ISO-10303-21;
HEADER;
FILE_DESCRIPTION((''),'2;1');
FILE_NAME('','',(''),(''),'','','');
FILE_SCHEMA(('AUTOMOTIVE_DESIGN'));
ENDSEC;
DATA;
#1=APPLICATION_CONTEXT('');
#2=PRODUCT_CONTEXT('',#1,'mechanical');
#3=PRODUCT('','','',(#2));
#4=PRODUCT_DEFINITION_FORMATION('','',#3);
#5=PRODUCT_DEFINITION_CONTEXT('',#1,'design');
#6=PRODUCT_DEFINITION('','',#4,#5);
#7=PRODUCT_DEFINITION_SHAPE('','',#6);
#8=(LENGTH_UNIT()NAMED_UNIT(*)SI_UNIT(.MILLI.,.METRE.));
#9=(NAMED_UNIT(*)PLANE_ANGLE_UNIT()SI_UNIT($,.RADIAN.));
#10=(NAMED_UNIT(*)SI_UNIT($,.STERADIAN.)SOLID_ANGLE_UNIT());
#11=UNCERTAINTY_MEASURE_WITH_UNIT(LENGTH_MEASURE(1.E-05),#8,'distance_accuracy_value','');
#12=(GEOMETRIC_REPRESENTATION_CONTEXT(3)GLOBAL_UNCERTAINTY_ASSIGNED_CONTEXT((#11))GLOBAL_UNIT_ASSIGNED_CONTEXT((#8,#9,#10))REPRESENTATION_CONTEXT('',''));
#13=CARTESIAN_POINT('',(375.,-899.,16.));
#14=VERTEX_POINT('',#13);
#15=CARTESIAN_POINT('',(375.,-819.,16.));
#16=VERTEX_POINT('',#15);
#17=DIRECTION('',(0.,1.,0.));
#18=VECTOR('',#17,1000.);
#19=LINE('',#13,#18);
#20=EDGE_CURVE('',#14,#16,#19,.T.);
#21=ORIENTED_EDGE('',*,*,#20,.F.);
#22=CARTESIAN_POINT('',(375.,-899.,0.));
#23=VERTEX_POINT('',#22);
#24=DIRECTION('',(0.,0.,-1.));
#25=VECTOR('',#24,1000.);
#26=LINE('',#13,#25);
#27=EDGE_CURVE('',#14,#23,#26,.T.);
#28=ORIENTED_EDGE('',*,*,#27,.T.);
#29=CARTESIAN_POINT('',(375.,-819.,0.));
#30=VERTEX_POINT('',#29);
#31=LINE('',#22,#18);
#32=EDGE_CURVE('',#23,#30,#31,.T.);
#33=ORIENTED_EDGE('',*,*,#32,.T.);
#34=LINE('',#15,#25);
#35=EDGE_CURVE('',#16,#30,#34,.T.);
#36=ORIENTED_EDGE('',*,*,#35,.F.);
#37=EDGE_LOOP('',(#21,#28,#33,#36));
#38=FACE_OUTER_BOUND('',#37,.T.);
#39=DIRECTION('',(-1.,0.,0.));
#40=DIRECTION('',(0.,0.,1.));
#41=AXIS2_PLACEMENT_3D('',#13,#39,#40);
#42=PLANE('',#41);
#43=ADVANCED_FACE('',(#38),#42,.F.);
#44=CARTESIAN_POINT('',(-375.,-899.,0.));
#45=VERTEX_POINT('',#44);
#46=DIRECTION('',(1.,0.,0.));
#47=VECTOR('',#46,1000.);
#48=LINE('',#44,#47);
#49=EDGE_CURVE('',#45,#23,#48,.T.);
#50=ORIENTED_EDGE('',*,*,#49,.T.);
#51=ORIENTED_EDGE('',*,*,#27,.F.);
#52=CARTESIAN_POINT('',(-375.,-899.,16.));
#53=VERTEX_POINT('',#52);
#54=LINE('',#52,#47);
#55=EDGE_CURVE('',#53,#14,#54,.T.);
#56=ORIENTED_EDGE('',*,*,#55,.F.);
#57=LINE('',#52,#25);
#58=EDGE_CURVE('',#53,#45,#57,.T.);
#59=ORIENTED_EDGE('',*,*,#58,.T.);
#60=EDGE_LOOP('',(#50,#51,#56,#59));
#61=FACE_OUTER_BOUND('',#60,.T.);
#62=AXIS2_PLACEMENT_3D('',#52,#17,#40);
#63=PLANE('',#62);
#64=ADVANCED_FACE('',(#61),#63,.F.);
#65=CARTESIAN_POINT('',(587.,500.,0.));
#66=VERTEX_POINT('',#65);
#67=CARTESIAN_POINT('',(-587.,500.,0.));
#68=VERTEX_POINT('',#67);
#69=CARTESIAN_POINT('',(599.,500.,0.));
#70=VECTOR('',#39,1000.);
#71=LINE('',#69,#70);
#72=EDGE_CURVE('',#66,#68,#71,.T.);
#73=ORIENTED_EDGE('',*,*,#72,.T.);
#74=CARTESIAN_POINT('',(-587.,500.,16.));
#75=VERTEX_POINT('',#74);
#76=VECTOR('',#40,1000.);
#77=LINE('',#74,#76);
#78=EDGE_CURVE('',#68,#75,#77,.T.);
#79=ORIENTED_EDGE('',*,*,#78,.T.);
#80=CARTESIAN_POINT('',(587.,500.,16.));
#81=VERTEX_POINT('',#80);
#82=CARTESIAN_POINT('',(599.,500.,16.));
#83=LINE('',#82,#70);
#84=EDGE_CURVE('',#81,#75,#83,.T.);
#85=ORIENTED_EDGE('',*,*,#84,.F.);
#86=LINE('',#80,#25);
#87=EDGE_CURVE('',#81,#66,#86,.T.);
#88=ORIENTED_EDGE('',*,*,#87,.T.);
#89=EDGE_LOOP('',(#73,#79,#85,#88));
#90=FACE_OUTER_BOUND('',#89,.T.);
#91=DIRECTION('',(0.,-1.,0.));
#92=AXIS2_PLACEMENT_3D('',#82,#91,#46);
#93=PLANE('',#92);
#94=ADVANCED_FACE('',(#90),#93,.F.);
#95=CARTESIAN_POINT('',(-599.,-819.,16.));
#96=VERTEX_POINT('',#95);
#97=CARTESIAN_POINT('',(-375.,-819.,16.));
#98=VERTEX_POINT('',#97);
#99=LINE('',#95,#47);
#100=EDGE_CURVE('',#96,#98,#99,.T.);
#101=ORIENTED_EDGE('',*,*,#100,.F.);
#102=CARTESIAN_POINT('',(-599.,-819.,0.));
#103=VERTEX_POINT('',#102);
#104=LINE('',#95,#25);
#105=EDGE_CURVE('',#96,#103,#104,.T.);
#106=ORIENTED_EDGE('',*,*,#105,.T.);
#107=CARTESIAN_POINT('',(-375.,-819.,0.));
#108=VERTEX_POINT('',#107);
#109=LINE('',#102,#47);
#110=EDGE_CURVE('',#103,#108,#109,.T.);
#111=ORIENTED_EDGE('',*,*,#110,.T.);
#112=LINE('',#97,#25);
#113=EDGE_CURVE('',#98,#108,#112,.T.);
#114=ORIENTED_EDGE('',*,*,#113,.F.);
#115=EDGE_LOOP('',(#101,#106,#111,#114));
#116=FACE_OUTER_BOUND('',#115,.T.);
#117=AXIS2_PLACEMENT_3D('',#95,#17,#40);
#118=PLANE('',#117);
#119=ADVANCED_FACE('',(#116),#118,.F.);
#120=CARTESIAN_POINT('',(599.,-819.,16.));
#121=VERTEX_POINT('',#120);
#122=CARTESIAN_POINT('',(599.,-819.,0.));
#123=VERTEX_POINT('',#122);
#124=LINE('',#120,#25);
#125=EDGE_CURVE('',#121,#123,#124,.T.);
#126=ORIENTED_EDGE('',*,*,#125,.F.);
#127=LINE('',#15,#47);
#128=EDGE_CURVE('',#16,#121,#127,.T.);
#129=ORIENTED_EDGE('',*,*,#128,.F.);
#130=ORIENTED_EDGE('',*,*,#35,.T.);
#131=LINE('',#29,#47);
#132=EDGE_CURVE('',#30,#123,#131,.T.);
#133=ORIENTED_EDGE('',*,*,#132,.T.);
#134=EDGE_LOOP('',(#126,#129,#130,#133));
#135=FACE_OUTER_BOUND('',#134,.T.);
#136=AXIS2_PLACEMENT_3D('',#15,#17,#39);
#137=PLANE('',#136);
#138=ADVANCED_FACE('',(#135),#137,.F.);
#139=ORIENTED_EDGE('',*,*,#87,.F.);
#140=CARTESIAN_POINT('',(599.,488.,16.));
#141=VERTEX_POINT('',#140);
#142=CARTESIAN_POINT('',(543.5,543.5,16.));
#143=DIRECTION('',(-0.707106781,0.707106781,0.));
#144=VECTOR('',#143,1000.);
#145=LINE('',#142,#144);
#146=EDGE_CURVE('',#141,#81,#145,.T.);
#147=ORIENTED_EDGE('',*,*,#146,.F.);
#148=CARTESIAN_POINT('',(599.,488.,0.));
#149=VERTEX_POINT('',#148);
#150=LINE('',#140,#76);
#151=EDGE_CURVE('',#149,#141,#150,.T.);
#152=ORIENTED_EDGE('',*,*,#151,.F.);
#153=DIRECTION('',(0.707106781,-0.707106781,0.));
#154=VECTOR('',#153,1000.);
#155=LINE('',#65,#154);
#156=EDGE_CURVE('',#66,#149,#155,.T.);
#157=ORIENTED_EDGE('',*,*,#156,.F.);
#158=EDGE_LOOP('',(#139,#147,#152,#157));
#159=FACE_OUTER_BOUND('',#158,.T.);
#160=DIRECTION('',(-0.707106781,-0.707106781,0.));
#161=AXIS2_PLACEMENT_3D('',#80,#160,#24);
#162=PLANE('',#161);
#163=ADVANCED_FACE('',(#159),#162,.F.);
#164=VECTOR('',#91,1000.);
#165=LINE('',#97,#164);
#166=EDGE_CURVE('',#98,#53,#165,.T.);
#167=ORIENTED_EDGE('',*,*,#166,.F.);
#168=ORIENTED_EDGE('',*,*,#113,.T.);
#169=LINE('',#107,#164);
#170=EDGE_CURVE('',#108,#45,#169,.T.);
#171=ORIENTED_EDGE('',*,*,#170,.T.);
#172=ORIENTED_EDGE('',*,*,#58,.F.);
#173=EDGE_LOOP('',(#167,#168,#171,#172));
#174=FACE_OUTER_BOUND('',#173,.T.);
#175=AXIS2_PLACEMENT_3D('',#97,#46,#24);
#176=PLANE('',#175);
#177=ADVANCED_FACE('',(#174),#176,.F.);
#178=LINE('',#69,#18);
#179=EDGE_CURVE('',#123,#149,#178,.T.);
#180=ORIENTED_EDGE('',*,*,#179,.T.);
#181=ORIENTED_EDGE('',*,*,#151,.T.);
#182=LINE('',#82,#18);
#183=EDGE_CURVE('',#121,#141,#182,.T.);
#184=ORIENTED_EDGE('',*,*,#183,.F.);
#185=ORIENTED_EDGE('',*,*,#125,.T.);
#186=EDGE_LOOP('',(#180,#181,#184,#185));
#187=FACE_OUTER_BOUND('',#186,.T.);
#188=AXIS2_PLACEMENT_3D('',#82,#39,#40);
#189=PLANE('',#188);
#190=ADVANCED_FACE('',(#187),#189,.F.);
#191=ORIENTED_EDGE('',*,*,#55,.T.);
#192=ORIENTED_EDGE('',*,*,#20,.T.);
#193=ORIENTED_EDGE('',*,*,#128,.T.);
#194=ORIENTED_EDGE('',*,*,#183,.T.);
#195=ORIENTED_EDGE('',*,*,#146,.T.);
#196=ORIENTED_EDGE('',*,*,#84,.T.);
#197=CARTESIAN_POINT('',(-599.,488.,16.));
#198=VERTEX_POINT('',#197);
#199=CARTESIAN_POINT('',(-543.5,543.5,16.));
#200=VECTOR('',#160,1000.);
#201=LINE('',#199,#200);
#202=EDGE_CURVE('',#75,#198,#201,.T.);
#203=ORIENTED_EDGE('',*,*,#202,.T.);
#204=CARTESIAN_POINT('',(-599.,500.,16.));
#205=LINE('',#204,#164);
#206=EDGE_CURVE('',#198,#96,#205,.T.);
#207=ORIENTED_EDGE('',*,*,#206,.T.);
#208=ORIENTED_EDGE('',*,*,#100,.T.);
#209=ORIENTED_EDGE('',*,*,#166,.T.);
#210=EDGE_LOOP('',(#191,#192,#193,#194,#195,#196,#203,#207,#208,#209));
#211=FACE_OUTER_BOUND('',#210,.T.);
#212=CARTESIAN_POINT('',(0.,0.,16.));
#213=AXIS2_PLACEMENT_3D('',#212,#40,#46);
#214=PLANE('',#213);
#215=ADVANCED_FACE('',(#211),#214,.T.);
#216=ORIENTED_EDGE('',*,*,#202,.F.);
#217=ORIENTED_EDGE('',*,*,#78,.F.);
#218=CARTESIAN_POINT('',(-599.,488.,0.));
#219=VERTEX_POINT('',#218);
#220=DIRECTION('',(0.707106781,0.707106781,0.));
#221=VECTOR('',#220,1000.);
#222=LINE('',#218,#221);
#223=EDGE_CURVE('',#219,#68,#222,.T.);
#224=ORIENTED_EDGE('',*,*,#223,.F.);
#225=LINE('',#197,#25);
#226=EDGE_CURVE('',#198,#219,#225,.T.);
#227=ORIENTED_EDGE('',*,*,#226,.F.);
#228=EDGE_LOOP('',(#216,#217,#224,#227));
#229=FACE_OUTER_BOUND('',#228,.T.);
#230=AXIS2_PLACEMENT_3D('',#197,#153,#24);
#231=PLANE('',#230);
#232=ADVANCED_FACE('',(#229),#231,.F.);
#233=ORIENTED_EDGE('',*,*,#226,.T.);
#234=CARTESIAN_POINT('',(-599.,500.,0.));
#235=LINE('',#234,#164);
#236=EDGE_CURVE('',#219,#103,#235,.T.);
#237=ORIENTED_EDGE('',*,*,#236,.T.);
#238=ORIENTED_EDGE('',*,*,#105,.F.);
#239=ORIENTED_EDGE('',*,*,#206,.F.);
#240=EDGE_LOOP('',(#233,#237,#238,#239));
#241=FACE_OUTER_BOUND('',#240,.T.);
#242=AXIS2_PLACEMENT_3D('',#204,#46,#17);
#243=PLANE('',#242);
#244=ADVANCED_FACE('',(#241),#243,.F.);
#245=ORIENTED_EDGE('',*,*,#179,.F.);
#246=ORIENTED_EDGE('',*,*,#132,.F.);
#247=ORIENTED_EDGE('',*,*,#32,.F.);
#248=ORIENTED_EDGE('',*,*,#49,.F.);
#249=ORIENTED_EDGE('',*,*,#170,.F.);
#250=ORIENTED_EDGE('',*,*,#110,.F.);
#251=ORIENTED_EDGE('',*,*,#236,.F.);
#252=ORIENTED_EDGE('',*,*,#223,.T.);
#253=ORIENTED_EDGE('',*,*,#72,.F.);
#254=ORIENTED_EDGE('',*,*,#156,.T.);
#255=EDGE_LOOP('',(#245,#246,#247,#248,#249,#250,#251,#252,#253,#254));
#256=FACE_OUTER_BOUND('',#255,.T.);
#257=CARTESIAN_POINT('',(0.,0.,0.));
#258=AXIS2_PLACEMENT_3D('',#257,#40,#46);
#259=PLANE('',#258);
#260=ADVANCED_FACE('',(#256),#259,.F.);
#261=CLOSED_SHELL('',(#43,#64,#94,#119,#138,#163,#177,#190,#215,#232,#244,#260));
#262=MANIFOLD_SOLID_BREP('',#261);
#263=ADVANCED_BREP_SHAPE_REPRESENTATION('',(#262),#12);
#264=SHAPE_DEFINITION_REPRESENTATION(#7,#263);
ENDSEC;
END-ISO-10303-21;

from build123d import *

# Parameters (mm, degrees)
EXTRUDE_1_DEPTH = 16
CHAMFER_1_SIZE  = 12


with BuildPart() as part:
    # 草图1 → 凸台-拉伸1 (new body)
    with BuildSketch(Plane.XY):
        Polygon((-599, -819), (-375, -819), (-375, -899), (375, -899), (375, -819), (599, -819), (599, 500), (-599, 500), align=None)
    extrude(amount=EXTRUDE_1_DEPTH)

    # 倒角1
    chamfer_1_edges = [part.edges().sort_by_distance(p)[0] for p in [
        (-599, 500, 8),
        (599, 500, 8),
    ]]
    chamfer(chamfer_1_edges, length=CHAMFER_1_SIZE)


solid = part.part
